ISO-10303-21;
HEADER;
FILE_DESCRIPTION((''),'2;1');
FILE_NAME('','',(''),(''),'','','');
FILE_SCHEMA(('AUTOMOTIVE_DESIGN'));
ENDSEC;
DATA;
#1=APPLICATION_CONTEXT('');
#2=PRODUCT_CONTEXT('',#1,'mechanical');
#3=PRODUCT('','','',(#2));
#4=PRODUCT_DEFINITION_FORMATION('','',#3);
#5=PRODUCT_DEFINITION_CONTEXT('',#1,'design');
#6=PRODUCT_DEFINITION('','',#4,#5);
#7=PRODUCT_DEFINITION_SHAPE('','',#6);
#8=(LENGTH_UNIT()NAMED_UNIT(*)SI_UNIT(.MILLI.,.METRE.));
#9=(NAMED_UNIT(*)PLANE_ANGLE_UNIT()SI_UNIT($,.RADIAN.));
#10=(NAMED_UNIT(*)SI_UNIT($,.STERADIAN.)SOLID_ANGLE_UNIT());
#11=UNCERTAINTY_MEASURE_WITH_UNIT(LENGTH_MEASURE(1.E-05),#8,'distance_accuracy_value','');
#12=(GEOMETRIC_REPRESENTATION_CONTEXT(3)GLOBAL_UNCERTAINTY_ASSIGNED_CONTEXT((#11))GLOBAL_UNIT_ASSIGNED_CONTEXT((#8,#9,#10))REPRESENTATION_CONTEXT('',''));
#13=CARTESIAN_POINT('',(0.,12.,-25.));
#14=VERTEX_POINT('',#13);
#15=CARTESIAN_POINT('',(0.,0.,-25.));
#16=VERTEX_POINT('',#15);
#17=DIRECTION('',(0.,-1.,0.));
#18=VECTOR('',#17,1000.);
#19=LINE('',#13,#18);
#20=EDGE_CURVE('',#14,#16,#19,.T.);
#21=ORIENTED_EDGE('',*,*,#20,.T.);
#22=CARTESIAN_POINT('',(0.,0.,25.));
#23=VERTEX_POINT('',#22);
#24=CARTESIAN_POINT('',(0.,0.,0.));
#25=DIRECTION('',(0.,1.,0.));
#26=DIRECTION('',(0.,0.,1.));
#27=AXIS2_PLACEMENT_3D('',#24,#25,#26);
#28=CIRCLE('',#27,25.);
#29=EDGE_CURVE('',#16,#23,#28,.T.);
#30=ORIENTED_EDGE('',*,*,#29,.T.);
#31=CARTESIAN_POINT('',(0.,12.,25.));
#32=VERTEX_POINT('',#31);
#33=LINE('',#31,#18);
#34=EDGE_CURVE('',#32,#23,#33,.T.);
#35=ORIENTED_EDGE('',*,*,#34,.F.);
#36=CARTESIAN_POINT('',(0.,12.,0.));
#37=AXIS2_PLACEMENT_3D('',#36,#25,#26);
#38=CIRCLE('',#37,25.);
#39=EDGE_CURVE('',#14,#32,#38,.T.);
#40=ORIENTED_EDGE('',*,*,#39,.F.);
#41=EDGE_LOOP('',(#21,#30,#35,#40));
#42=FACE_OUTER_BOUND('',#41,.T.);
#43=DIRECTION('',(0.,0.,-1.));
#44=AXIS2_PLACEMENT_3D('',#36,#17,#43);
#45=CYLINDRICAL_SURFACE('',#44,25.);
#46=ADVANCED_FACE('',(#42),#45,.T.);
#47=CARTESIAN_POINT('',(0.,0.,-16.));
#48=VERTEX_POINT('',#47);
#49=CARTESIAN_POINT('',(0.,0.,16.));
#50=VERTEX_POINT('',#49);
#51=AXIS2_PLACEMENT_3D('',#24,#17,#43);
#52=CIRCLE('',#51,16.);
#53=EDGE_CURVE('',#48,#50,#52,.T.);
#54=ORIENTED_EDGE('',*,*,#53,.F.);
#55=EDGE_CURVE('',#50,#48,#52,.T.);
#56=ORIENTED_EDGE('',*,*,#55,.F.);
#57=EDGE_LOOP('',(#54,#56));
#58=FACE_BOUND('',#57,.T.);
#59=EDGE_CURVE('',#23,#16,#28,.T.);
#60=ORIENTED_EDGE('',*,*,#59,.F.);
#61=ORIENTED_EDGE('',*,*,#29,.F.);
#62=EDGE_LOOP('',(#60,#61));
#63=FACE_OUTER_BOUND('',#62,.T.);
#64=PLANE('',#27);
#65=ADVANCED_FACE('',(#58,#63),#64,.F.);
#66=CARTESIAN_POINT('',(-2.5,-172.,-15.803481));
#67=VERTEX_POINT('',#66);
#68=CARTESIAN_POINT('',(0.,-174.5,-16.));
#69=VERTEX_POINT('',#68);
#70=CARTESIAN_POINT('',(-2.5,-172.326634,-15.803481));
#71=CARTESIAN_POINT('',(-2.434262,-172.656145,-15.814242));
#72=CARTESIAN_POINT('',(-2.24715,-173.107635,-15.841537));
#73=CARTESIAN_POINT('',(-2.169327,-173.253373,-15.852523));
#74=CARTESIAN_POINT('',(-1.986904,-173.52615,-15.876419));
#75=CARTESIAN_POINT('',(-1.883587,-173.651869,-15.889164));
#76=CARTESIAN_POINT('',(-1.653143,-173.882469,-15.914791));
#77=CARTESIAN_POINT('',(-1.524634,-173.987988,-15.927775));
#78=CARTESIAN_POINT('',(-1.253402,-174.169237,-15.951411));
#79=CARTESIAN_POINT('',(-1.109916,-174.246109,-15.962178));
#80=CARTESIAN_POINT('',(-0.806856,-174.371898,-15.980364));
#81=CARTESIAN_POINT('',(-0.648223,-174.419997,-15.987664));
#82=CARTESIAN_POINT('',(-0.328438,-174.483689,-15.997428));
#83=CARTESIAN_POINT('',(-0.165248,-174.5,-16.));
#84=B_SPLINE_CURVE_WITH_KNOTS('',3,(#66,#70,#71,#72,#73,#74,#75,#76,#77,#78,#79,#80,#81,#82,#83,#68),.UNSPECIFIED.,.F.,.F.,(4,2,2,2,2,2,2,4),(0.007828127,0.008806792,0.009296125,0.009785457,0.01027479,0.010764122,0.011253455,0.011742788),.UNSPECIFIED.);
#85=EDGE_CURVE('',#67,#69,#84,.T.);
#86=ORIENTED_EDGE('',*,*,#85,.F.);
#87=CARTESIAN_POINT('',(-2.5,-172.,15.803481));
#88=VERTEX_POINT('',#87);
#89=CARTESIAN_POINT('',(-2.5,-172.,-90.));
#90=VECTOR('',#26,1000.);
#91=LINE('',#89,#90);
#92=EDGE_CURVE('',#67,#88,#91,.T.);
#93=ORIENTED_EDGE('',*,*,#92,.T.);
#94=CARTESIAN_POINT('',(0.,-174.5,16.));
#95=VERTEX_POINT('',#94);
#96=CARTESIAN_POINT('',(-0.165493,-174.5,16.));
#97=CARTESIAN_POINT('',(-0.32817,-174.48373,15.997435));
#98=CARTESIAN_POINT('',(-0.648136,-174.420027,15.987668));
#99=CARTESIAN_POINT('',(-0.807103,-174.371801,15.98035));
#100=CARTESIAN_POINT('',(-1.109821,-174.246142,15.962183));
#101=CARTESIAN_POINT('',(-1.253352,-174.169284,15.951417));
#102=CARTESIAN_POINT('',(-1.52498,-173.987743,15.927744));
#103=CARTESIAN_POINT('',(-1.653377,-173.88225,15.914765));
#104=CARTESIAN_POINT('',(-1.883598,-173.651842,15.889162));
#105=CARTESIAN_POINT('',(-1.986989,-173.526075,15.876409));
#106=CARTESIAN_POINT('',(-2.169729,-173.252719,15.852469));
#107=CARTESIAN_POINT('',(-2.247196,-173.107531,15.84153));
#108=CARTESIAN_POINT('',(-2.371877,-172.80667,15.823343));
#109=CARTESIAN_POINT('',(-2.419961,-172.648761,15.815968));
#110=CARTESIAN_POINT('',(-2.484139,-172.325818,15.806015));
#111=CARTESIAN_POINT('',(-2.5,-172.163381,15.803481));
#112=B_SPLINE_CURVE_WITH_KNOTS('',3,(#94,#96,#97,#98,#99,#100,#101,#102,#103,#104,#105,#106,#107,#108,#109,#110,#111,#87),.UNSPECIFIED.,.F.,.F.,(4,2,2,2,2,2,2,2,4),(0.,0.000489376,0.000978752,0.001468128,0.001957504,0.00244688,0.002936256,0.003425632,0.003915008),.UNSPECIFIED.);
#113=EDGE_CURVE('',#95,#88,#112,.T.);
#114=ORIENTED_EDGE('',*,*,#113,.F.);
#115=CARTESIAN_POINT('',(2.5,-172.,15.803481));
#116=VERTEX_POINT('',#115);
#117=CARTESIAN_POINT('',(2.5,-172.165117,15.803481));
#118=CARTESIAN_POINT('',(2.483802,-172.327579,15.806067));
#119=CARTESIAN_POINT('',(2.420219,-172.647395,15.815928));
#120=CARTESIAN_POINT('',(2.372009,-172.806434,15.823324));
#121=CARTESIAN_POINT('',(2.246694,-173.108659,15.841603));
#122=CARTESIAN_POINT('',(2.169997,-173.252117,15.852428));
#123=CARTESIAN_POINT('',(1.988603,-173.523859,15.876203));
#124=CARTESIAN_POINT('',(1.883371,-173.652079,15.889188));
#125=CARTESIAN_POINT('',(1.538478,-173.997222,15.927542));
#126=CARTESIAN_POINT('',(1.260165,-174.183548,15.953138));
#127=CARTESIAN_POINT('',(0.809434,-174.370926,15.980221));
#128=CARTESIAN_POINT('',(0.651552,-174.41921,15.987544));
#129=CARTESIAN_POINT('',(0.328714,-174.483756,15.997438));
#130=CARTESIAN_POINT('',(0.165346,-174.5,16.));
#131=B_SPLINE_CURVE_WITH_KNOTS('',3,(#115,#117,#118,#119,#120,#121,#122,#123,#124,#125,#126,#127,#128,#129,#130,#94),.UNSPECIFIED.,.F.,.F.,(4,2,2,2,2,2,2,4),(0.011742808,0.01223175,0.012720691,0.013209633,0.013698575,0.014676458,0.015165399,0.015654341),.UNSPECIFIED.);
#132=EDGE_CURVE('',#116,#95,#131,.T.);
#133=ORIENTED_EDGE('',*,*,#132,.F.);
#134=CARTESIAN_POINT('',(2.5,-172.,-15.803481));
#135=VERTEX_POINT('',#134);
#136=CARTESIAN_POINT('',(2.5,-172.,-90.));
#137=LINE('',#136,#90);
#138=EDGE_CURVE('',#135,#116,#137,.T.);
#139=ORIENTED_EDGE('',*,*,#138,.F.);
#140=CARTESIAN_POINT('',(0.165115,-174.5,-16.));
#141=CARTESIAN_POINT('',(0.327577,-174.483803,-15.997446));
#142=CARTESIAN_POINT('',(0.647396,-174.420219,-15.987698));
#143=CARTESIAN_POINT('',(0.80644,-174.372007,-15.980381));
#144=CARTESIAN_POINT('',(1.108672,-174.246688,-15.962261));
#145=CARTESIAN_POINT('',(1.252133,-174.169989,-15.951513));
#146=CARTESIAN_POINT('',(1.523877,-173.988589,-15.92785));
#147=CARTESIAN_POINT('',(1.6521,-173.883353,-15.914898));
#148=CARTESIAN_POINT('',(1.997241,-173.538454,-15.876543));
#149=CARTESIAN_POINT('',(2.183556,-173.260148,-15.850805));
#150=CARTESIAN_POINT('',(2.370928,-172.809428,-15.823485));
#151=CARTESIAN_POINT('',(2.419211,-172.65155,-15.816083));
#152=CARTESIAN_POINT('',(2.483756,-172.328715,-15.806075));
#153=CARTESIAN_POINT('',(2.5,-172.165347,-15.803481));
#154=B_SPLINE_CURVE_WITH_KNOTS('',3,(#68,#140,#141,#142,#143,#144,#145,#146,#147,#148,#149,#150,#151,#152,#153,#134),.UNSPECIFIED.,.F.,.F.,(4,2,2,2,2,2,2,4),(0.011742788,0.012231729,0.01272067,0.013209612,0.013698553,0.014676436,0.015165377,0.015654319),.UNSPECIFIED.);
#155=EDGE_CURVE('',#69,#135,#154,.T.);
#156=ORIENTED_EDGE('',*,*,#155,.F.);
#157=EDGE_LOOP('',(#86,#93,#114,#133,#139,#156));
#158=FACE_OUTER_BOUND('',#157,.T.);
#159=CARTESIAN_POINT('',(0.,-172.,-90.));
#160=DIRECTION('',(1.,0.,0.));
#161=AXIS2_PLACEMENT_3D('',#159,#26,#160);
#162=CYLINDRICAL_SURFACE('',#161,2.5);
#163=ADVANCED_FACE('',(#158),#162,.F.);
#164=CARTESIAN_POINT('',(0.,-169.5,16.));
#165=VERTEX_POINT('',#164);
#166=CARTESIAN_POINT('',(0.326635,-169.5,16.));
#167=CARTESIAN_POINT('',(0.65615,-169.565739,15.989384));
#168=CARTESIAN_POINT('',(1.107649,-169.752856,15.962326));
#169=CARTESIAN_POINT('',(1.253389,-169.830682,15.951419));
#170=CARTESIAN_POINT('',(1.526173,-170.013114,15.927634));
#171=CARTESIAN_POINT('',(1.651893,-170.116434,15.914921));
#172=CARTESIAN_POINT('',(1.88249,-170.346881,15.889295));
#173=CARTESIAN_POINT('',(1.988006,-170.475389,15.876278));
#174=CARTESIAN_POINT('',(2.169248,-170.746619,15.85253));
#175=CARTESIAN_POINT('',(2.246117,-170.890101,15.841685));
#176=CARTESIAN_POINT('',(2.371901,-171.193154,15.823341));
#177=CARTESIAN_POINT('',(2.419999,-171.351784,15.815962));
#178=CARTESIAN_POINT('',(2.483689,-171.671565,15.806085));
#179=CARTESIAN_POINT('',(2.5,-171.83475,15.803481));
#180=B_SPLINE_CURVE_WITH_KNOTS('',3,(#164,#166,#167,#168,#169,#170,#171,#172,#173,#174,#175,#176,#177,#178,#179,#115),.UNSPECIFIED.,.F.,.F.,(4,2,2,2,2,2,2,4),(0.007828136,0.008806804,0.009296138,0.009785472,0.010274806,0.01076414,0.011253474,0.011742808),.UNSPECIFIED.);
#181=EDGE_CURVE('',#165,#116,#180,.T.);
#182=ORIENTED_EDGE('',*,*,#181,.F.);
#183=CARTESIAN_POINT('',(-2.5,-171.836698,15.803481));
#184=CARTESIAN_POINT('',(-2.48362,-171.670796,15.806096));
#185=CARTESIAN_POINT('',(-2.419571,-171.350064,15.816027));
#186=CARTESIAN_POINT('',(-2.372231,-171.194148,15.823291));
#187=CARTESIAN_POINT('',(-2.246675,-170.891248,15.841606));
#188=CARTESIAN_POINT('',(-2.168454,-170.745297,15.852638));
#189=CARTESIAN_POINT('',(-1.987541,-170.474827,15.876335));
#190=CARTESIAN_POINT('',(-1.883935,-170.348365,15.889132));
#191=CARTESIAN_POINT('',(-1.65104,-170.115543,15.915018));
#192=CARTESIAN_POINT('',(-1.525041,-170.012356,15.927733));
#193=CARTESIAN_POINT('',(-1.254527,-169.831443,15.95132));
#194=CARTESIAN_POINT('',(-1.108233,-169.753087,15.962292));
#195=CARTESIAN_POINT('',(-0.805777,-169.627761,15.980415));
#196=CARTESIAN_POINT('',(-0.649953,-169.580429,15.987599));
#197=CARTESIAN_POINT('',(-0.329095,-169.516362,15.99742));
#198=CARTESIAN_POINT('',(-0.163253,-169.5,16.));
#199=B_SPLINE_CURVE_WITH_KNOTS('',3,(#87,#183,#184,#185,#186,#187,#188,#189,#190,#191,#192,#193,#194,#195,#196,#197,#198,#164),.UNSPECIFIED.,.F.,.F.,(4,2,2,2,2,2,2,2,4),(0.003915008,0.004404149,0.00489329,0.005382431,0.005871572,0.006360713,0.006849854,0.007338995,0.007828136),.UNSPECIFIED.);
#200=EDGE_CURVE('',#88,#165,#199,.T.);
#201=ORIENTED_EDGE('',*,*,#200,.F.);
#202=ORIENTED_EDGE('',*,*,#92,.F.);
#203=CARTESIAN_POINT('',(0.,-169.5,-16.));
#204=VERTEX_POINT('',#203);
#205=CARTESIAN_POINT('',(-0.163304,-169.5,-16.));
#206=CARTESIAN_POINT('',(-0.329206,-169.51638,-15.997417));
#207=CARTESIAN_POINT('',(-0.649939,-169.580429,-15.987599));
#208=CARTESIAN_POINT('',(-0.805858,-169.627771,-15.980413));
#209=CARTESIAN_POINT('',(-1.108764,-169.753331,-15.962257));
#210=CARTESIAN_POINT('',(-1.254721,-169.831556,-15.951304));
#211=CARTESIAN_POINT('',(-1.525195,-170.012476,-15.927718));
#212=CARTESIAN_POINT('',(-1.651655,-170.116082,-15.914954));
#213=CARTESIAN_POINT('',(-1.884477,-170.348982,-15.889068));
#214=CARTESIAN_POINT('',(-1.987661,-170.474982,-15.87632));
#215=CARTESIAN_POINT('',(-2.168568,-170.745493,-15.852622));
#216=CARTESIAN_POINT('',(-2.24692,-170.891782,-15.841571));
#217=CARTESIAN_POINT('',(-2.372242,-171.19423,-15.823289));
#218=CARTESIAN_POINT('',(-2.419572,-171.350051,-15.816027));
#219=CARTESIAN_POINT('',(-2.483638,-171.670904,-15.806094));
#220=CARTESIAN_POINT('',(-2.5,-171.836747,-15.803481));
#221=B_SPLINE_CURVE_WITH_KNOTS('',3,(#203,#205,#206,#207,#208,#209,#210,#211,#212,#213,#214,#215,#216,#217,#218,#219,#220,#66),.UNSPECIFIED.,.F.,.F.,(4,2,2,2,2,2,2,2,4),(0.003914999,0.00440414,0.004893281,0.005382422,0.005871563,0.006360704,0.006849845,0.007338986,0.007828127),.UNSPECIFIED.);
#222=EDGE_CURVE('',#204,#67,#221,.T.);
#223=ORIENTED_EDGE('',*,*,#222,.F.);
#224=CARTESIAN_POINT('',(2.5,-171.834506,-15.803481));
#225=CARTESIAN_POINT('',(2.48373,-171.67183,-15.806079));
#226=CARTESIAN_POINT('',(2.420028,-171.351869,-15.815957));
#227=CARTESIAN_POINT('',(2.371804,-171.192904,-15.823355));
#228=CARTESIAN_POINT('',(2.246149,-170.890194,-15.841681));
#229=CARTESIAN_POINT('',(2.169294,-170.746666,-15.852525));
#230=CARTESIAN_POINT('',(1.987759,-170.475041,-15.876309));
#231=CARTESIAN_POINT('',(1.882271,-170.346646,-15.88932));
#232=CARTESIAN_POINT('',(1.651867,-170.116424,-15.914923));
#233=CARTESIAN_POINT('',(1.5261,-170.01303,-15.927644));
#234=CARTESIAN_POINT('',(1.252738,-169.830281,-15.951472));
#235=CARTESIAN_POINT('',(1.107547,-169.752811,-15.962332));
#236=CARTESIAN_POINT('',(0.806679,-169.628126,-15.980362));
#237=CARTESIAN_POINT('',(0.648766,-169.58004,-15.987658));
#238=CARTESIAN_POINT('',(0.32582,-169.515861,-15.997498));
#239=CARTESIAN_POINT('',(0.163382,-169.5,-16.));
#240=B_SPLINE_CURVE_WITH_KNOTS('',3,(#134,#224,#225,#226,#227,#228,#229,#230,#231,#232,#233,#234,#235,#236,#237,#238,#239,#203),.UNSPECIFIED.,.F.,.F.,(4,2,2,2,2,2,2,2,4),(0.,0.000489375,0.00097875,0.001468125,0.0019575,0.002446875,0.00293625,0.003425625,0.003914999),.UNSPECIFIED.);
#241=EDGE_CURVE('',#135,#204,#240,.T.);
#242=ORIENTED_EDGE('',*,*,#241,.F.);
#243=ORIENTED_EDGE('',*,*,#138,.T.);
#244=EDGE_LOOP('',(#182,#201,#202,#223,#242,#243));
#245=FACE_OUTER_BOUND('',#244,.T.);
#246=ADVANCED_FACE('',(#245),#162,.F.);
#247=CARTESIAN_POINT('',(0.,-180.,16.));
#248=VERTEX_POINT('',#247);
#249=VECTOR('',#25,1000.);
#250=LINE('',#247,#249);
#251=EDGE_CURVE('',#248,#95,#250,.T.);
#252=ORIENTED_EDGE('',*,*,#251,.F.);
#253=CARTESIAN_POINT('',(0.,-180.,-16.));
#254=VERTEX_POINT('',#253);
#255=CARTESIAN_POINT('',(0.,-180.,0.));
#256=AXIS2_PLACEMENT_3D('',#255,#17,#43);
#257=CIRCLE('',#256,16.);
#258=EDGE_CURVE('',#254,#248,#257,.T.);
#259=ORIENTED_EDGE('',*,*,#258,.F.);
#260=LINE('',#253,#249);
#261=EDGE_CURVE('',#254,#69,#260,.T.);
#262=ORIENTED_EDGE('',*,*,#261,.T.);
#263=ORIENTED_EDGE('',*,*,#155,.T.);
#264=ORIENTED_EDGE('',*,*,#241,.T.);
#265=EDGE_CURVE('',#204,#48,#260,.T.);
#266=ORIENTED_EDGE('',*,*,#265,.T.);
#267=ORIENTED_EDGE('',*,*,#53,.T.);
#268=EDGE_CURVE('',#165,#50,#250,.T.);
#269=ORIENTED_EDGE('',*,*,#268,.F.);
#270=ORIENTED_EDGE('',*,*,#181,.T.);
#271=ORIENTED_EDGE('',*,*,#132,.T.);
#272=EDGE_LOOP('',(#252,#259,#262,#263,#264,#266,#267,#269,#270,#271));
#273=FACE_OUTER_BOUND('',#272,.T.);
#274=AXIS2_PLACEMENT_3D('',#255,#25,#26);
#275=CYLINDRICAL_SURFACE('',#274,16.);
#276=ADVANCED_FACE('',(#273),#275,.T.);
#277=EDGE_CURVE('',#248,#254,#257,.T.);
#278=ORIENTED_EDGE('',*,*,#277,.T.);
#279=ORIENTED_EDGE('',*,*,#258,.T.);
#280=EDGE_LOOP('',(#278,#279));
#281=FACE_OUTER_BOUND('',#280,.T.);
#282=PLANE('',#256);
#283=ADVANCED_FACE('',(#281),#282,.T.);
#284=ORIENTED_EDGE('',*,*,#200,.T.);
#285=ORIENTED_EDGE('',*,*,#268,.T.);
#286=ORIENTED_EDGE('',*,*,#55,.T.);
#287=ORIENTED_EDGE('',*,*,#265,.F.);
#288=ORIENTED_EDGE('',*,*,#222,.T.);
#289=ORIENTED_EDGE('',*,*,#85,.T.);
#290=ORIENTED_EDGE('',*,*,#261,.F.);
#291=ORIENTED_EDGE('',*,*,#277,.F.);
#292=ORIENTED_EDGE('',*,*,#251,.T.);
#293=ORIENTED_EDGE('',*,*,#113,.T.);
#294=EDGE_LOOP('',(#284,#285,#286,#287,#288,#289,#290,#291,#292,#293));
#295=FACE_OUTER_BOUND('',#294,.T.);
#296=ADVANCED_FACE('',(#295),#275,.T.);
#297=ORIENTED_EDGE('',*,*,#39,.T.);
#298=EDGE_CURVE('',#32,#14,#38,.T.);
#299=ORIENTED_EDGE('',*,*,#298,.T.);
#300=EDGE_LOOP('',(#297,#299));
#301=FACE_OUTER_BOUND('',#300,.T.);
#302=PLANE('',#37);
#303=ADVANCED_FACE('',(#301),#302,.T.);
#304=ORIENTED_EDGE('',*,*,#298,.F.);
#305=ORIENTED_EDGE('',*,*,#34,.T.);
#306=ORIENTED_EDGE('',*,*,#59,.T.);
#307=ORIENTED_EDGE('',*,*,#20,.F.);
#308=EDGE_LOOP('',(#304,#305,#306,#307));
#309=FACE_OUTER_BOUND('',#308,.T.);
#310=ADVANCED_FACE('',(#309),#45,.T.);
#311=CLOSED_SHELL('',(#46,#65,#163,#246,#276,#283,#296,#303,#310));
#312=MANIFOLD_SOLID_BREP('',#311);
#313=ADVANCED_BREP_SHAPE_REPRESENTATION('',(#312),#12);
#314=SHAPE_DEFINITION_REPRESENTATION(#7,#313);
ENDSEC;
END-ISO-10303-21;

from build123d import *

# Parameters (mm, degrees)
HEAD_PROFILE_SKETCH_R  = 25
HEAD_50X12_DEPTH       = 12
SHANK_PROFILE_SKETCH_R = 16
SHANK_32X180_DEPTH     = 180
CROSS_HOLE_SKETCH_R    = 2.5
CROSS_HOLE_5_DEPTH     = 90


with BuildPart() as part:
    # Head Profile Sketch → Head Ø50x12 (new body)
    with BuildSketch(Plane(origin=(0, 0, 0), x_dir=(1, 0, 0), z_dir=(0, 1, 0))):
        with Locations(Location((0, 0, 0), (0, 0, 270))):
            Circle(HEAD_PROFILE_SKETCH_R)
    extrude(amount=HEAD_50X12_DEPTH)

    # Shank Profile Sketch → Shank Ø32x180 (add)
    with BuildSketch(Plane.XZ):
        with Locations(Location((0, 0, 0), (0, 0, 90))):
            Circle(SHANK_PROFILE_SKETCH_R)
    extrude(amount=SHANK_32X180_DEPTH)

    # Cross Hole Sketch → Cross Hole Ø5 (cut, symmetric)
    with BuildSketch(Plane.XY):
        with Locations(Location((0, -172, 0), (0, 0, 270.000000048))):
            Circle(CROSS_HOLE_SKETCH_R)
    extrude(amount=CROSS_HOLE_5_DEPTH, both=True, mode=Mode.SUBTRACT)


solid = part.part
